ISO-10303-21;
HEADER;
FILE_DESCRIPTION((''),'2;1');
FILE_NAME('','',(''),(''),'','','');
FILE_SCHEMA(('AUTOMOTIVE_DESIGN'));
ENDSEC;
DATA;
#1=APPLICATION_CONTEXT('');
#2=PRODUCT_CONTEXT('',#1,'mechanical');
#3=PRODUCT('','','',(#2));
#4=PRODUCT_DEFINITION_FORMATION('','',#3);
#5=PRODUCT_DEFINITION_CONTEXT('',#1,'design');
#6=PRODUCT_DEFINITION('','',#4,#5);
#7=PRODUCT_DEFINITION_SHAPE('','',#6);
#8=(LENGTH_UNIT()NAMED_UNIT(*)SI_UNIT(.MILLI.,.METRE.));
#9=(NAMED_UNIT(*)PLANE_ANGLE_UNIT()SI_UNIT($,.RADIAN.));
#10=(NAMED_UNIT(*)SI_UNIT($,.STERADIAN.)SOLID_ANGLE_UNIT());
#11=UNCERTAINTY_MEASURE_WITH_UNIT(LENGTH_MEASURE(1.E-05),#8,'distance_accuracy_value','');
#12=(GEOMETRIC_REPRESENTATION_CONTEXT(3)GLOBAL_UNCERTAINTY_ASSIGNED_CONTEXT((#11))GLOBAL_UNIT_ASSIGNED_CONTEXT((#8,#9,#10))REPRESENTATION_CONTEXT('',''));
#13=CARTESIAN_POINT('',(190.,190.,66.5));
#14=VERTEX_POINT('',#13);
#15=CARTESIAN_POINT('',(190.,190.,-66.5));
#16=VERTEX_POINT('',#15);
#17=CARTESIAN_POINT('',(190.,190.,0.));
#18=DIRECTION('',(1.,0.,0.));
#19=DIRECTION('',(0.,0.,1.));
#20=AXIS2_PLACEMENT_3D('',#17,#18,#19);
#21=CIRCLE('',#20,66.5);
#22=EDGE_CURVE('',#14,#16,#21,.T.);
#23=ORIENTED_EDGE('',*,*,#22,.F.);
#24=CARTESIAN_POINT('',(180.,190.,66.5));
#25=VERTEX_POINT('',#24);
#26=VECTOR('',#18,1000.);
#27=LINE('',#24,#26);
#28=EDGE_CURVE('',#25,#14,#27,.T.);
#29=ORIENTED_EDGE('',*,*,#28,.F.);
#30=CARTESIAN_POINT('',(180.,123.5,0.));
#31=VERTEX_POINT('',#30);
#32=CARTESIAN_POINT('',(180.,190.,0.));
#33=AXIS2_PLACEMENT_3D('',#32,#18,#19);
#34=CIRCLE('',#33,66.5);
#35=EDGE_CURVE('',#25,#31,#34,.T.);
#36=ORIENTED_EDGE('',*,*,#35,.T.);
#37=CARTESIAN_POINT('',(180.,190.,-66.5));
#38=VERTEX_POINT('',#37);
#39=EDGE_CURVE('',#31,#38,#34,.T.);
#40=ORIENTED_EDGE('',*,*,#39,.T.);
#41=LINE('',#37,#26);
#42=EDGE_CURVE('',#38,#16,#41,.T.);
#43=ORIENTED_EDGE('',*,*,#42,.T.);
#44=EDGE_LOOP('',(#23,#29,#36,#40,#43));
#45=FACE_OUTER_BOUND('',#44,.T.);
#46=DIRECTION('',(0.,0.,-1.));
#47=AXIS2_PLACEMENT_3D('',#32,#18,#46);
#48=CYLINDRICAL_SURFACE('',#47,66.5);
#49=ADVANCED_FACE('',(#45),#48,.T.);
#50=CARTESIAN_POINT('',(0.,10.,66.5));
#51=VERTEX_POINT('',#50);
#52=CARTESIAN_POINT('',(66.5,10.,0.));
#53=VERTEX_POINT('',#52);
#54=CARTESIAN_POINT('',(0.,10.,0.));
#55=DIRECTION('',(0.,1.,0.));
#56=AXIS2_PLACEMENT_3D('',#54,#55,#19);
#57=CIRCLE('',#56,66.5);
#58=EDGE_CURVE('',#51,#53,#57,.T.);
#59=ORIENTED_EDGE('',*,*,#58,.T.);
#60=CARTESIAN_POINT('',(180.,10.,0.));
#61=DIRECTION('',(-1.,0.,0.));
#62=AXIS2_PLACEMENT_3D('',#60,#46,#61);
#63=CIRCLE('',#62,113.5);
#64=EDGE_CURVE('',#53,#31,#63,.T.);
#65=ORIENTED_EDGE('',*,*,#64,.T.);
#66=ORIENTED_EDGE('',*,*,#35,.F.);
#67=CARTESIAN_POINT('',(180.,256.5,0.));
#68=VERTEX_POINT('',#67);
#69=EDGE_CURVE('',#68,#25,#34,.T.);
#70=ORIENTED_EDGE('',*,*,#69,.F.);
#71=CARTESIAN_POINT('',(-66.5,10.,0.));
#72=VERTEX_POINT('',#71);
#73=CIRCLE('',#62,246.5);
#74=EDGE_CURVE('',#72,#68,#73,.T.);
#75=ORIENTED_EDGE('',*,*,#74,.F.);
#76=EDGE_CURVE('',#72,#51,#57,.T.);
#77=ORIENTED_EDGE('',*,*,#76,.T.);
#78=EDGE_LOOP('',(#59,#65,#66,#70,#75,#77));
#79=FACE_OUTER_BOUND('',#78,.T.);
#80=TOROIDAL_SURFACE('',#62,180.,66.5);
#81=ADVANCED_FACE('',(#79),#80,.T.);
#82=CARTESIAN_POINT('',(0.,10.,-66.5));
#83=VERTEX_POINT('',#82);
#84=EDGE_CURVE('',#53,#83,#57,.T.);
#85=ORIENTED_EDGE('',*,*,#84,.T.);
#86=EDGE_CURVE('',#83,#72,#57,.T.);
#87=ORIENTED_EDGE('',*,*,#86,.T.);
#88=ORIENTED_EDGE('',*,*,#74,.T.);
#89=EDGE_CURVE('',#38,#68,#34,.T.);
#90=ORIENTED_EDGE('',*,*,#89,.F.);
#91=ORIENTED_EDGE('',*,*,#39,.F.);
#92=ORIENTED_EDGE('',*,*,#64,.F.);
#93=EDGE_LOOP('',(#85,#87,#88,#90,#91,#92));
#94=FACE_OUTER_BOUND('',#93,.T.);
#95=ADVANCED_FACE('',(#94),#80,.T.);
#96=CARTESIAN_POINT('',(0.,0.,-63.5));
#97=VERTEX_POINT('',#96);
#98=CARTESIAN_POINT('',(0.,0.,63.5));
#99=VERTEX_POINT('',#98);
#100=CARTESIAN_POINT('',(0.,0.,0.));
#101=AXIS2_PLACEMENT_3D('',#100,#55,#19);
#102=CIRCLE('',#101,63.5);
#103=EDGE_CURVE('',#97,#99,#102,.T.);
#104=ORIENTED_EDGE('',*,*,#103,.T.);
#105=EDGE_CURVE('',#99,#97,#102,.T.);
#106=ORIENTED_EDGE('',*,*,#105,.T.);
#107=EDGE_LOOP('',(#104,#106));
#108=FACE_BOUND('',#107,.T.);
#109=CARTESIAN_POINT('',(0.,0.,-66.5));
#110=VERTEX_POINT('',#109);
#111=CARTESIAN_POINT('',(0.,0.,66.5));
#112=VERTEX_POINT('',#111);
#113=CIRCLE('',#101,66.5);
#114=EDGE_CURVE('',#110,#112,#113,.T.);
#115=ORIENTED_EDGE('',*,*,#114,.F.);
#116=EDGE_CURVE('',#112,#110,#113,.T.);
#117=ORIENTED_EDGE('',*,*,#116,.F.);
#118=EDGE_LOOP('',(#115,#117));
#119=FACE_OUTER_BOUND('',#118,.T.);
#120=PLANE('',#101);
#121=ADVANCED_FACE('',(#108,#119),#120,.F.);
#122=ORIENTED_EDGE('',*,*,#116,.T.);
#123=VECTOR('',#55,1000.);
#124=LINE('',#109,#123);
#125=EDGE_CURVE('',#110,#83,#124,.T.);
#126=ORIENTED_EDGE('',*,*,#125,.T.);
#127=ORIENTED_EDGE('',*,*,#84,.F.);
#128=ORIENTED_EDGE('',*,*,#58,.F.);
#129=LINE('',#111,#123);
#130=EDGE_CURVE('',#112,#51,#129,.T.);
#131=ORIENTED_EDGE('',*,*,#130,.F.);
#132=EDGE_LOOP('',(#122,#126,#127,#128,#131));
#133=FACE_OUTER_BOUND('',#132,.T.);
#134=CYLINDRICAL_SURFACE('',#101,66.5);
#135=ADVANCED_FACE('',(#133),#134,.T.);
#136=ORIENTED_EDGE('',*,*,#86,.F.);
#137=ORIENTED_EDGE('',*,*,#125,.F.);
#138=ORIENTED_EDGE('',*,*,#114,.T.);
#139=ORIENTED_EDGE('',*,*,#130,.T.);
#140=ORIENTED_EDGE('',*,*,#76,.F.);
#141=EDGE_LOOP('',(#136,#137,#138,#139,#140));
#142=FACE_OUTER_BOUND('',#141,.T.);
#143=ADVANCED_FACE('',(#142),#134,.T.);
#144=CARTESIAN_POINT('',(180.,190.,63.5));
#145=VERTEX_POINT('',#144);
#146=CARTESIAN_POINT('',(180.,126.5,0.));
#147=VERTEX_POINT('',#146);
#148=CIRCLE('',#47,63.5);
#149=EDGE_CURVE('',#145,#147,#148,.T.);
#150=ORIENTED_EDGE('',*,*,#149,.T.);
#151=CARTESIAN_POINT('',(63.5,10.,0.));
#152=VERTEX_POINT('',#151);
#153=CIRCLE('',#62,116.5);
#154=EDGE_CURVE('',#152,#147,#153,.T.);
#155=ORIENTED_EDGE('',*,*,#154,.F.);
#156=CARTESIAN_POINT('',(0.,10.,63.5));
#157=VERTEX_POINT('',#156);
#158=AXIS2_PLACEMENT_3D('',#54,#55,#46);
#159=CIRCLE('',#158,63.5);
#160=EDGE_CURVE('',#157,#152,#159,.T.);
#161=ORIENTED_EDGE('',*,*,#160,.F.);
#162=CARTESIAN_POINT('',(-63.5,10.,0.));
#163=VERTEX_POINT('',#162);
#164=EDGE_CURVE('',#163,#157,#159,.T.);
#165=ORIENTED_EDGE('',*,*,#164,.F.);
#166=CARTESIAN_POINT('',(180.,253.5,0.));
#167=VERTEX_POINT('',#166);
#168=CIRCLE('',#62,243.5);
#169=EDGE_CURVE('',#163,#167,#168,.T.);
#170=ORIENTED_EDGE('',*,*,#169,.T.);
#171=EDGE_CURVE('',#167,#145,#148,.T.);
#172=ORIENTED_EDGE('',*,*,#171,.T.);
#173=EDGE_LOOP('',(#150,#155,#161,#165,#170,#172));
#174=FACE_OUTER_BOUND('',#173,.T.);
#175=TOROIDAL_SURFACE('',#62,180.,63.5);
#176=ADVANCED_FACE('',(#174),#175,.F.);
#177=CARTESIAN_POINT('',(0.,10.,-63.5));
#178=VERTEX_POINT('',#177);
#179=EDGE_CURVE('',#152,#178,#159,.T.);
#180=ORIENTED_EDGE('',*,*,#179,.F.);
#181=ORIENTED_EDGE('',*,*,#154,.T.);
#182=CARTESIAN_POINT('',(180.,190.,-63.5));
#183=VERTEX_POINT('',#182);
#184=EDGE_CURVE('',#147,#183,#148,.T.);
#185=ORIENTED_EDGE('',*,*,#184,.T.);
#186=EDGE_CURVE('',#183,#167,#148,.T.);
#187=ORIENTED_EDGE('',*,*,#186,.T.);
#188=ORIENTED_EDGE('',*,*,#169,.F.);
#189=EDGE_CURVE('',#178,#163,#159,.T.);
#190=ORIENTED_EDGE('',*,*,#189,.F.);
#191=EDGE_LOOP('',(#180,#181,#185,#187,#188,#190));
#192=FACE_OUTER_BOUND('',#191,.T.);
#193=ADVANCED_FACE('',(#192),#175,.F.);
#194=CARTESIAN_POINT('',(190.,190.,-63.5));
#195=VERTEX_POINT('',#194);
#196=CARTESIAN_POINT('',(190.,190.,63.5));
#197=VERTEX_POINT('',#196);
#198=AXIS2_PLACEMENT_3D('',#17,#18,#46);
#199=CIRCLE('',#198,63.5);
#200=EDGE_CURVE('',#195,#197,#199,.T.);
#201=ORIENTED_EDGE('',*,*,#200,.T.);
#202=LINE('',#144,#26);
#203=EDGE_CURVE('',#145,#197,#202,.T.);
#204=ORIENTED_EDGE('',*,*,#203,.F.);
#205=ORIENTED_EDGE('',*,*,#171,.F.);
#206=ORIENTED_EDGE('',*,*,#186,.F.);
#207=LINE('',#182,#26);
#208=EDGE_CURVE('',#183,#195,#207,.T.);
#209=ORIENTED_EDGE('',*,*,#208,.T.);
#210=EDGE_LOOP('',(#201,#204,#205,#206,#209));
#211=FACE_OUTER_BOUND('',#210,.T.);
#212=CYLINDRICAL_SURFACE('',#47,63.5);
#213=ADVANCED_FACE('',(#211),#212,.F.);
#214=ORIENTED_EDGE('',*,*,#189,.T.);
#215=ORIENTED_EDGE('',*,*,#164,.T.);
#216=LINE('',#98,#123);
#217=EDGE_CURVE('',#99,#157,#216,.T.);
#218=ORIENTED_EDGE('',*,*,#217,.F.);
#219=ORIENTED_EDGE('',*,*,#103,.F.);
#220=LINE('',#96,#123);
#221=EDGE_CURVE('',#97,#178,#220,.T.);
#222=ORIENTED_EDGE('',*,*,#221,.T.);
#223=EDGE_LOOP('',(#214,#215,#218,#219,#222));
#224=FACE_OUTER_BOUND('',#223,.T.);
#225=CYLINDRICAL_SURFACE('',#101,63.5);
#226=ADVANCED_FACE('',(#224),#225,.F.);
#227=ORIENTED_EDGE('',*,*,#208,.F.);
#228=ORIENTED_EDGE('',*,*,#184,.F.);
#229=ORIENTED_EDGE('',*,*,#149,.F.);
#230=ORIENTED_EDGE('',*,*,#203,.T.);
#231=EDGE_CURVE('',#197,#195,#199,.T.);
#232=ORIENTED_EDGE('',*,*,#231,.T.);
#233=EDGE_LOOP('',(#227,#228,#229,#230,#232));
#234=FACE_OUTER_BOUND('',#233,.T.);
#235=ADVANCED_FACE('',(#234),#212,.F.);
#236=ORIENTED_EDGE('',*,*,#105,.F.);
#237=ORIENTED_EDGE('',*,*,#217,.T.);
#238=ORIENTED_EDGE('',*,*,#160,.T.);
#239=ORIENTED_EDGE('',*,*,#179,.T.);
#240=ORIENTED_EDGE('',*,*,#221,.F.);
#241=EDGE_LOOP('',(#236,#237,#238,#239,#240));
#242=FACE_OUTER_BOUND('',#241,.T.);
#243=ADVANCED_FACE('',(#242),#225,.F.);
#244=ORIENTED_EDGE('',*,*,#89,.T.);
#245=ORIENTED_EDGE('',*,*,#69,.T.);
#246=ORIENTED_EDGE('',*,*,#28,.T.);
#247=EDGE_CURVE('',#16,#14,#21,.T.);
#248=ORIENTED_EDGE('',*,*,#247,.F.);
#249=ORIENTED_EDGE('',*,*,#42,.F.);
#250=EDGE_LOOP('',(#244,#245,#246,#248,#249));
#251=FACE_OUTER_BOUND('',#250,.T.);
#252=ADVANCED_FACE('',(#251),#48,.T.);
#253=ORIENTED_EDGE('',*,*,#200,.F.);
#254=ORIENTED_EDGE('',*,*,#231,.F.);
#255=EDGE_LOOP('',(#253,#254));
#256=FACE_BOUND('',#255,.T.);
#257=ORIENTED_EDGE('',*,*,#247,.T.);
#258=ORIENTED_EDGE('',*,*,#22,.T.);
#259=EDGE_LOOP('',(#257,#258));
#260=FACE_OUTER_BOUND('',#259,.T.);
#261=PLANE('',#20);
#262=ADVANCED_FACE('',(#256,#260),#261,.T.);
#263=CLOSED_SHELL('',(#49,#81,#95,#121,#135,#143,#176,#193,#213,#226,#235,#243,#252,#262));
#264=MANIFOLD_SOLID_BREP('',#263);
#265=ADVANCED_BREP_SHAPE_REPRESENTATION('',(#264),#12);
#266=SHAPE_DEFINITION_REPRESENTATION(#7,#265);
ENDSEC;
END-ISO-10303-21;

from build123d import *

# Parameters (mm, degrees)
SKETCH1_R = 66.5
SHELL1_T  = -3


with BuildPart() as part:
    # Sweep1: sweep along a path in Sketch2
    with BuildLine(Plane.XY) as sweep1_path:
        Line((0, 0), (0, 10))
        ThreePointArc((0, 10), (52.720779386, 137.279220614), (180, 190))
        Line((180, 190), (190, 190))
    # Sketch1 → Sweep1 (sweep)
    with BuildSketch(Plane(origin=(0, 0, 0), x_dir=(1, 0, 0), z_dir=(0, 1, 0))):
        Circle(SKETCH1_R)
    sweep(path=sweep1_path.line)

    # Shell1
    shell1_openings = [part.faces().sort_by_distance(p)[0] for p in [
        (190, 190, 0),
        (0, 0, 0),
    ]]
    offset(amount=SHELL1_T, openings=shell1_openings, kind=Kind.INTERSECTION)


solid = part.part
